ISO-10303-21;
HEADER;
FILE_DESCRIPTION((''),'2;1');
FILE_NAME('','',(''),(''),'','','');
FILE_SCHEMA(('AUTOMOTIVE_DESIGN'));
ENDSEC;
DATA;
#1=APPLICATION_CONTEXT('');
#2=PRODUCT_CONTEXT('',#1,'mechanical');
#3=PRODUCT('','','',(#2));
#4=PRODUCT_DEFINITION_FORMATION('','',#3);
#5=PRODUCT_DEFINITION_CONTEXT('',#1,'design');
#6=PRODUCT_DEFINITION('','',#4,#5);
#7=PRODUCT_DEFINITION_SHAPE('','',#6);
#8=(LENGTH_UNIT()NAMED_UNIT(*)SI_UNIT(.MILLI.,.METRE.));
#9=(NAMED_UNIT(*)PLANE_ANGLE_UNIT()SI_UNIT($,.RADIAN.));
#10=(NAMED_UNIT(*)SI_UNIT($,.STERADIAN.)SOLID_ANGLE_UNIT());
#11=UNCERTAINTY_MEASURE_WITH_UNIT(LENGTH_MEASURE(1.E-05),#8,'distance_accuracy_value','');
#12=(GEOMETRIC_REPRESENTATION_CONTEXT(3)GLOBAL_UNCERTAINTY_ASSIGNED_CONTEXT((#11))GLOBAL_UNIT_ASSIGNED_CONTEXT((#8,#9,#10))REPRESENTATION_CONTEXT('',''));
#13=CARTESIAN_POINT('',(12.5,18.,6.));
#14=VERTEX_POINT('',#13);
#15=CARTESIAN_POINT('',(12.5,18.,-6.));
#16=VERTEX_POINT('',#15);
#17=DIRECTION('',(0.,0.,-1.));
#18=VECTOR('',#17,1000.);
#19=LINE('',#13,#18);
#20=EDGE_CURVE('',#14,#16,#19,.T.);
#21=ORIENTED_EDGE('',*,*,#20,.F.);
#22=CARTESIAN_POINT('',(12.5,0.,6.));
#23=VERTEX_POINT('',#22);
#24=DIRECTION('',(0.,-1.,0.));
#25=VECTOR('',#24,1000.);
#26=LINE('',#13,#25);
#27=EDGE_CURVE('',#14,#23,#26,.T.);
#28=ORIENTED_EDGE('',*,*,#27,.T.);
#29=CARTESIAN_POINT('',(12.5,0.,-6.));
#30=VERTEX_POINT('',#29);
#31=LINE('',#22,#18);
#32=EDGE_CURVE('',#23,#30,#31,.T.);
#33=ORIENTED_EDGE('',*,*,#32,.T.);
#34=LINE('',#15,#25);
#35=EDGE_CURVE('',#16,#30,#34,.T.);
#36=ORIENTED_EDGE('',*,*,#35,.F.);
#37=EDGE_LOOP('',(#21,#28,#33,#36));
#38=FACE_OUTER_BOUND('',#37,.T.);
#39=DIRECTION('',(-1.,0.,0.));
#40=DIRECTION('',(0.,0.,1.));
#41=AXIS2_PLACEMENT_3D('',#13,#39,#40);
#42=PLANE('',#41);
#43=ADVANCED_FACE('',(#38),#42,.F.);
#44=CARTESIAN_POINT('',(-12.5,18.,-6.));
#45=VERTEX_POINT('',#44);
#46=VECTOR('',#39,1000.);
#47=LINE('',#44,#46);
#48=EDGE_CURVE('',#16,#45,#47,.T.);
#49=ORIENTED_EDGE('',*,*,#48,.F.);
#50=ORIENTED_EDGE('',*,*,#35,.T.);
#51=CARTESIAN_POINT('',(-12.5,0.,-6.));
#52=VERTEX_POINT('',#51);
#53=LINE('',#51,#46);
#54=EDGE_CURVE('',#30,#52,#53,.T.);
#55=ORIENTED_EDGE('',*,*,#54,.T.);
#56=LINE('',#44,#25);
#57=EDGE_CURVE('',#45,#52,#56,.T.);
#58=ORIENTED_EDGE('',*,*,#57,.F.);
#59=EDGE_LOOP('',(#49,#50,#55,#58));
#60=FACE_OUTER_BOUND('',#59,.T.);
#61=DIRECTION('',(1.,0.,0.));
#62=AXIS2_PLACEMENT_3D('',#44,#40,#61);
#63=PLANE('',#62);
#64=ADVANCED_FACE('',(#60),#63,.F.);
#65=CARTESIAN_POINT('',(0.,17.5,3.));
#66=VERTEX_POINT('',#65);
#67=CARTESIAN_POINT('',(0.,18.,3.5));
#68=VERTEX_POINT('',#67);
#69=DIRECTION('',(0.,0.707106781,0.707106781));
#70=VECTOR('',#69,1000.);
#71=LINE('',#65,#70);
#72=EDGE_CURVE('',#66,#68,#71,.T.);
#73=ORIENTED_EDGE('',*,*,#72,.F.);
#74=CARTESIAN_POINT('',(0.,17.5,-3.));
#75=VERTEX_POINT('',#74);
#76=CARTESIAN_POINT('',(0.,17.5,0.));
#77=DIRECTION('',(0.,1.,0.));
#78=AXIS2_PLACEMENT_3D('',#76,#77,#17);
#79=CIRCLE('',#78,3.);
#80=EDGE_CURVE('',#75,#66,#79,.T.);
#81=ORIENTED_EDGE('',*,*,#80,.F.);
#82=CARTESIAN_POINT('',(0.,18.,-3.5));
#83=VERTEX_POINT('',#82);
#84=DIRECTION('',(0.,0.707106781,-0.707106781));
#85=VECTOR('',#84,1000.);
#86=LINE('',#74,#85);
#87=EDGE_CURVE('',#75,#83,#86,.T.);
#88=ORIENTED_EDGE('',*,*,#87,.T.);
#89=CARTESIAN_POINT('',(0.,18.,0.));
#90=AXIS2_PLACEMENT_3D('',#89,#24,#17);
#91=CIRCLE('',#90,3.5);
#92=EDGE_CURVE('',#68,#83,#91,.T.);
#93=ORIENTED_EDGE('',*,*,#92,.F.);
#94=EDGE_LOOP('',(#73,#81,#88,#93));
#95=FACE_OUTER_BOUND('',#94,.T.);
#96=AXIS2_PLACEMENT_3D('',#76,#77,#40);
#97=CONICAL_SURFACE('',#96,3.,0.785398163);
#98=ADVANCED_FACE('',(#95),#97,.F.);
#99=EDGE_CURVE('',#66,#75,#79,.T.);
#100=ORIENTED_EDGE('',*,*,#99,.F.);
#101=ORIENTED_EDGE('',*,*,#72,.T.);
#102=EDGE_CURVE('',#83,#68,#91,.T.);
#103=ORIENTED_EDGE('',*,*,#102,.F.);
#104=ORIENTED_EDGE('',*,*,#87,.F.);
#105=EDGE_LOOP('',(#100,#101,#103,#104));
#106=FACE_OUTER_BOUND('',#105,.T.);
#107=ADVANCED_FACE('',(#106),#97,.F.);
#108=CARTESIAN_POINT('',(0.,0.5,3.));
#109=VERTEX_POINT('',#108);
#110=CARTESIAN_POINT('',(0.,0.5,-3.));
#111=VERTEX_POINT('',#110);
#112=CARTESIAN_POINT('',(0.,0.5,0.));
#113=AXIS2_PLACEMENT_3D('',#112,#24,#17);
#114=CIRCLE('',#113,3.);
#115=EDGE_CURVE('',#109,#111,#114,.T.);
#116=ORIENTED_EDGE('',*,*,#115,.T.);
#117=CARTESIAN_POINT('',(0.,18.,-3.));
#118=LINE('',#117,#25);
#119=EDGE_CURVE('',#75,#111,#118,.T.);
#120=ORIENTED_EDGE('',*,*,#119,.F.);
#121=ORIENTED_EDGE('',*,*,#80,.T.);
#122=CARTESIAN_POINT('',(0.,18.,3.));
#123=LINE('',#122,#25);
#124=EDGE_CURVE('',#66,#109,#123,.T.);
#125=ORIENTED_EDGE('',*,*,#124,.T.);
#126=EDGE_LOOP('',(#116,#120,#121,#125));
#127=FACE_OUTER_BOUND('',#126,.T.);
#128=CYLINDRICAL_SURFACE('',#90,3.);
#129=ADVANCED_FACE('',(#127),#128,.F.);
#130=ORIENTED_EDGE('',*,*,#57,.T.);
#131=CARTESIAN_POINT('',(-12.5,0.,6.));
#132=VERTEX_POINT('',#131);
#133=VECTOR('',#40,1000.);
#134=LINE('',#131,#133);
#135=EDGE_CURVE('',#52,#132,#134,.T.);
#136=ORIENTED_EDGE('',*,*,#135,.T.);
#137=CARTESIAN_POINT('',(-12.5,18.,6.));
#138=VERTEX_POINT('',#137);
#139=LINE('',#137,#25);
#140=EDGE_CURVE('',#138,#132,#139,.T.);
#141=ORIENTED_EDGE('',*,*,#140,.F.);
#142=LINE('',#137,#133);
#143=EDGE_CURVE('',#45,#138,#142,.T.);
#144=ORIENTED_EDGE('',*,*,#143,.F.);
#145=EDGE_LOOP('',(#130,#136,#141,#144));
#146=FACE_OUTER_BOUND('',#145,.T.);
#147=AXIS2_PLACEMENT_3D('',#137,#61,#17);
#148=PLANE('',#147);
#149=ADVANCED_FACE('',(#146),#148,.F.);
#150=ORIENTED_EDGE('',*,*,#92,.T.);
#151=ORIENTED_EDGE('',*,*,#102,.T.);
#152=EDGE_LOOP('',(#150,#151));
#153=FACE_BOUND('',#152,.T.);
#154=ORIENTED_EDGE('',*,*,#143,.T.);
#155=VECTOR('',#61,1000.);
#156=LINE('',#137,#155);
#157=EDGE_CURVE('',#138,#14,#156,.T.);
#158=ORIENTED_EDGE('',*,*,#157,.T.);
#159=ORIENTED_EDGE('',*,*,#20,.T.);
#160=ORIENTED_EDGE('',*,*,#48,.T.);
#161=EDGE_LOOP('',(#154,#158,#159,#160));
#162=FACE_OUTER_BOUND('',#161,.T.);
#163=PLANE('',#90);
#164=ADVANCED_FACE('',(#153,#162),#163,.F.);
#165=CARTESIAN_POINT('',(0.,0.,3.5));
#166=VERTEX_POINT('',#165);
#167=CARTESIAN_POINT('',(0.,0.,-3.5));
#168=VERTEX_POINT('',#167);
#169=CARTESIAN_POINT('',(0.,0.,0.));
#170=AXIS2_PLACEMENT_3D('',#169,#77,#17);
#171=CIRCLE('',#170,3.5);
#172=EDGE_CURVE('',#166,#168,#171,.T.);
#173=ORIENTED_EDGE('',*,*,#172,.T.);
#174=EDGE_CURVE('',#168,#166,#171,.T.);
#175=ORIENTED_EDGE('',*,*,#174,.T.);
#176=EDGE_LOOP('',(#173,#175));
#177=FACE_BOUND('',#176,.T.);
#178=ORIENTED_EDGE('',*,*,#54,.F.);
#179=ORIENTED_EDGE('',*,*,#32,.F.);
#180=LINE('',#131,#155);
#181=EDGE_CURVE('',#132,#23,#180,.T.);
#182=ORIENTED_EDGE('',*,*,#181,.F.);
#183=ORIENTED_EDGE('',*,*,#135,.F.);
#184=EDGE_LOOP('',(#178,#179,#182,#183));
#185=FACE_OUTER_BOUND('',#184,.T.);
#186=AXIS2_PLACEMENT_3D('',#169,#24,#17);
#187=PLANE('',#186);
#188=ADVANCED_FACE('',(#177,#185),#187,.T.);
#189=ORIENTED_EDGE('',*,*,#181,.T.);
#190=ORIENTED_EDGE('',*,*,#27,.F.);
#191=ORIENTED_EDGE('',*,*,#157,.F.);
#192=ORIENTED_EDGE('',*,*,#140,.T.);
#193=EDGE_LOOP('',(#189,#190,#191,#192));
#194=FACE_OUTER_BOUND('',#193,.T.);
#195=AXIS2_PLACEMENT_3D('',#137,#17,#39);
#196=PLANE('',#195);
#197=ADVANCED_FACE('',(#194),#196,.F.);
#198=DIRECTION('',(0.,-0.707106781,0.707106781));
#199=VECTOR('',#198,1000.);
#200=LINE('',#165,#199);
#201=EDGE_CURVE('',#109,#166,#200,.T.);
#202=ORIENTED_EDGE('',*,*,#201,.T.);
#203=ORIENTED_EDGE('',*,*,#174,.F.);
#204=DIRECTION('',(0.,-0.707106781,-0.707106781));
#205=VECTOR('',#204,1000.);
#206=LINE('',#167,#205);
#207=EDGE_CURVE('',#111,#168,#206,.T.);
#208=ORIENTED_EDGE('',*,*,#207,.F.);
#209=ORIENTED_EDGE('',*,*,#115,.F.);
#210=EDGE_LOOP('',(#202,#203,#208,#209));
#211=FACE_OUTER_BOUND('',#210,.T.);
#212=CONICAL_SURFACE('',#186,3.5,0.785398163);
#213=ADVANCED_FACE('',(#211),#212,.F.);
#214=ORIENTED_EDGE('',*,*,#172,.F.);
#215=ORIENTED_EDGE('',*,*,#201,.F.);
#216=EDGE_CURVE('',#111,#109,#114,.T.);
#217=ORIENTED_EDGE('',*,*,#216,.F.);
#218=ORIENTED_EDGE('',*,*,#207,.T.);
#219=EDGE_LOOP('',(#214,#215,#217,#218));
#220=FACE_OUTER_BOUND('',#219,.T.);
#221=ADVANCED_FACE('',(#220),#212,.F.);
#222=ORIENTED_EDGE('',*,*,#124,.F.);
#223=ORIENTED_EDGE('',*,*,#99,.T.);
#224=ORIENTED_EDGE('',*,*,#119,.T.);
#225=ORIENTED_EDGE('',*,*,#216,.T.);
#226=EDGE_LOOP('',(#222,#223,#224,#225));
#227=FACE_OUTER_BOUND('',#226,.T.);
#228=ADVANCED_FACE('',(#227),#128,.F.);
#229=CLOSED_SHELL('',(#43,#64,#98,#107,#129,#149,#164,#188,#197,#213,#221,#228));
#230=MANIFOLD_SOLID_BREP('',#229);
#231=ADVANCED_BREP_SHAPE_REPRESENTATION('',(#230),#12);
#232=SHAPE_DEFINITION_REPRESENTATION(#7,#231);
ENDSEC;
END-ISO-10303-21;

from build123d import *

# Parameters (mm, degrees)
SKETCH1_W           = 25
SKETCH1_H           = 12
BOSS_EXTRUDE1_DEPTH = 18
SKETCH2_R           = 3
CUT_EXTRUDE1_DEPTH  = 23.721135535
CHAMFER1_SIZE       = 0.5


with BuildPart() as part:
    # Sketch1 → Boss-Extrude1 (new body)
    with BuildSketch(Plane(origin=(0, 0, 0), x_dir=(1, 0, 0), z_dir=(0, 1, 0))):
        Rectangle(SKETCH1_W, SKETCH1_H)
    extrude(amount=BOSS_EXTRUDE1_DEPTH)

    # Sketch2 → Cut-Extrude1 (cut, through all)
    with BuildSketch(Plane(origin=(0, 0, 0), x_dir=(1, 0, 0), z_dir=(0, 1, 0))):
        with Locations(Location((0, 0, 0), (0, 0, 270))):
            Circle(SKETCH2_R)
    extrude(amount=CUT_EXTRUDE1_DEPTH, mode=Mode.SUBTRACT)

    # Chamfer1
    chamfer1_edges = [part.edges().sort_by_distance(p)[0] for p in [
        (0, 0, -3),
        (0, 18, -3),
    ]]
    chamfer(chamfer1_edges, length=CHAMFER1_SIZE)


solid = part.part
